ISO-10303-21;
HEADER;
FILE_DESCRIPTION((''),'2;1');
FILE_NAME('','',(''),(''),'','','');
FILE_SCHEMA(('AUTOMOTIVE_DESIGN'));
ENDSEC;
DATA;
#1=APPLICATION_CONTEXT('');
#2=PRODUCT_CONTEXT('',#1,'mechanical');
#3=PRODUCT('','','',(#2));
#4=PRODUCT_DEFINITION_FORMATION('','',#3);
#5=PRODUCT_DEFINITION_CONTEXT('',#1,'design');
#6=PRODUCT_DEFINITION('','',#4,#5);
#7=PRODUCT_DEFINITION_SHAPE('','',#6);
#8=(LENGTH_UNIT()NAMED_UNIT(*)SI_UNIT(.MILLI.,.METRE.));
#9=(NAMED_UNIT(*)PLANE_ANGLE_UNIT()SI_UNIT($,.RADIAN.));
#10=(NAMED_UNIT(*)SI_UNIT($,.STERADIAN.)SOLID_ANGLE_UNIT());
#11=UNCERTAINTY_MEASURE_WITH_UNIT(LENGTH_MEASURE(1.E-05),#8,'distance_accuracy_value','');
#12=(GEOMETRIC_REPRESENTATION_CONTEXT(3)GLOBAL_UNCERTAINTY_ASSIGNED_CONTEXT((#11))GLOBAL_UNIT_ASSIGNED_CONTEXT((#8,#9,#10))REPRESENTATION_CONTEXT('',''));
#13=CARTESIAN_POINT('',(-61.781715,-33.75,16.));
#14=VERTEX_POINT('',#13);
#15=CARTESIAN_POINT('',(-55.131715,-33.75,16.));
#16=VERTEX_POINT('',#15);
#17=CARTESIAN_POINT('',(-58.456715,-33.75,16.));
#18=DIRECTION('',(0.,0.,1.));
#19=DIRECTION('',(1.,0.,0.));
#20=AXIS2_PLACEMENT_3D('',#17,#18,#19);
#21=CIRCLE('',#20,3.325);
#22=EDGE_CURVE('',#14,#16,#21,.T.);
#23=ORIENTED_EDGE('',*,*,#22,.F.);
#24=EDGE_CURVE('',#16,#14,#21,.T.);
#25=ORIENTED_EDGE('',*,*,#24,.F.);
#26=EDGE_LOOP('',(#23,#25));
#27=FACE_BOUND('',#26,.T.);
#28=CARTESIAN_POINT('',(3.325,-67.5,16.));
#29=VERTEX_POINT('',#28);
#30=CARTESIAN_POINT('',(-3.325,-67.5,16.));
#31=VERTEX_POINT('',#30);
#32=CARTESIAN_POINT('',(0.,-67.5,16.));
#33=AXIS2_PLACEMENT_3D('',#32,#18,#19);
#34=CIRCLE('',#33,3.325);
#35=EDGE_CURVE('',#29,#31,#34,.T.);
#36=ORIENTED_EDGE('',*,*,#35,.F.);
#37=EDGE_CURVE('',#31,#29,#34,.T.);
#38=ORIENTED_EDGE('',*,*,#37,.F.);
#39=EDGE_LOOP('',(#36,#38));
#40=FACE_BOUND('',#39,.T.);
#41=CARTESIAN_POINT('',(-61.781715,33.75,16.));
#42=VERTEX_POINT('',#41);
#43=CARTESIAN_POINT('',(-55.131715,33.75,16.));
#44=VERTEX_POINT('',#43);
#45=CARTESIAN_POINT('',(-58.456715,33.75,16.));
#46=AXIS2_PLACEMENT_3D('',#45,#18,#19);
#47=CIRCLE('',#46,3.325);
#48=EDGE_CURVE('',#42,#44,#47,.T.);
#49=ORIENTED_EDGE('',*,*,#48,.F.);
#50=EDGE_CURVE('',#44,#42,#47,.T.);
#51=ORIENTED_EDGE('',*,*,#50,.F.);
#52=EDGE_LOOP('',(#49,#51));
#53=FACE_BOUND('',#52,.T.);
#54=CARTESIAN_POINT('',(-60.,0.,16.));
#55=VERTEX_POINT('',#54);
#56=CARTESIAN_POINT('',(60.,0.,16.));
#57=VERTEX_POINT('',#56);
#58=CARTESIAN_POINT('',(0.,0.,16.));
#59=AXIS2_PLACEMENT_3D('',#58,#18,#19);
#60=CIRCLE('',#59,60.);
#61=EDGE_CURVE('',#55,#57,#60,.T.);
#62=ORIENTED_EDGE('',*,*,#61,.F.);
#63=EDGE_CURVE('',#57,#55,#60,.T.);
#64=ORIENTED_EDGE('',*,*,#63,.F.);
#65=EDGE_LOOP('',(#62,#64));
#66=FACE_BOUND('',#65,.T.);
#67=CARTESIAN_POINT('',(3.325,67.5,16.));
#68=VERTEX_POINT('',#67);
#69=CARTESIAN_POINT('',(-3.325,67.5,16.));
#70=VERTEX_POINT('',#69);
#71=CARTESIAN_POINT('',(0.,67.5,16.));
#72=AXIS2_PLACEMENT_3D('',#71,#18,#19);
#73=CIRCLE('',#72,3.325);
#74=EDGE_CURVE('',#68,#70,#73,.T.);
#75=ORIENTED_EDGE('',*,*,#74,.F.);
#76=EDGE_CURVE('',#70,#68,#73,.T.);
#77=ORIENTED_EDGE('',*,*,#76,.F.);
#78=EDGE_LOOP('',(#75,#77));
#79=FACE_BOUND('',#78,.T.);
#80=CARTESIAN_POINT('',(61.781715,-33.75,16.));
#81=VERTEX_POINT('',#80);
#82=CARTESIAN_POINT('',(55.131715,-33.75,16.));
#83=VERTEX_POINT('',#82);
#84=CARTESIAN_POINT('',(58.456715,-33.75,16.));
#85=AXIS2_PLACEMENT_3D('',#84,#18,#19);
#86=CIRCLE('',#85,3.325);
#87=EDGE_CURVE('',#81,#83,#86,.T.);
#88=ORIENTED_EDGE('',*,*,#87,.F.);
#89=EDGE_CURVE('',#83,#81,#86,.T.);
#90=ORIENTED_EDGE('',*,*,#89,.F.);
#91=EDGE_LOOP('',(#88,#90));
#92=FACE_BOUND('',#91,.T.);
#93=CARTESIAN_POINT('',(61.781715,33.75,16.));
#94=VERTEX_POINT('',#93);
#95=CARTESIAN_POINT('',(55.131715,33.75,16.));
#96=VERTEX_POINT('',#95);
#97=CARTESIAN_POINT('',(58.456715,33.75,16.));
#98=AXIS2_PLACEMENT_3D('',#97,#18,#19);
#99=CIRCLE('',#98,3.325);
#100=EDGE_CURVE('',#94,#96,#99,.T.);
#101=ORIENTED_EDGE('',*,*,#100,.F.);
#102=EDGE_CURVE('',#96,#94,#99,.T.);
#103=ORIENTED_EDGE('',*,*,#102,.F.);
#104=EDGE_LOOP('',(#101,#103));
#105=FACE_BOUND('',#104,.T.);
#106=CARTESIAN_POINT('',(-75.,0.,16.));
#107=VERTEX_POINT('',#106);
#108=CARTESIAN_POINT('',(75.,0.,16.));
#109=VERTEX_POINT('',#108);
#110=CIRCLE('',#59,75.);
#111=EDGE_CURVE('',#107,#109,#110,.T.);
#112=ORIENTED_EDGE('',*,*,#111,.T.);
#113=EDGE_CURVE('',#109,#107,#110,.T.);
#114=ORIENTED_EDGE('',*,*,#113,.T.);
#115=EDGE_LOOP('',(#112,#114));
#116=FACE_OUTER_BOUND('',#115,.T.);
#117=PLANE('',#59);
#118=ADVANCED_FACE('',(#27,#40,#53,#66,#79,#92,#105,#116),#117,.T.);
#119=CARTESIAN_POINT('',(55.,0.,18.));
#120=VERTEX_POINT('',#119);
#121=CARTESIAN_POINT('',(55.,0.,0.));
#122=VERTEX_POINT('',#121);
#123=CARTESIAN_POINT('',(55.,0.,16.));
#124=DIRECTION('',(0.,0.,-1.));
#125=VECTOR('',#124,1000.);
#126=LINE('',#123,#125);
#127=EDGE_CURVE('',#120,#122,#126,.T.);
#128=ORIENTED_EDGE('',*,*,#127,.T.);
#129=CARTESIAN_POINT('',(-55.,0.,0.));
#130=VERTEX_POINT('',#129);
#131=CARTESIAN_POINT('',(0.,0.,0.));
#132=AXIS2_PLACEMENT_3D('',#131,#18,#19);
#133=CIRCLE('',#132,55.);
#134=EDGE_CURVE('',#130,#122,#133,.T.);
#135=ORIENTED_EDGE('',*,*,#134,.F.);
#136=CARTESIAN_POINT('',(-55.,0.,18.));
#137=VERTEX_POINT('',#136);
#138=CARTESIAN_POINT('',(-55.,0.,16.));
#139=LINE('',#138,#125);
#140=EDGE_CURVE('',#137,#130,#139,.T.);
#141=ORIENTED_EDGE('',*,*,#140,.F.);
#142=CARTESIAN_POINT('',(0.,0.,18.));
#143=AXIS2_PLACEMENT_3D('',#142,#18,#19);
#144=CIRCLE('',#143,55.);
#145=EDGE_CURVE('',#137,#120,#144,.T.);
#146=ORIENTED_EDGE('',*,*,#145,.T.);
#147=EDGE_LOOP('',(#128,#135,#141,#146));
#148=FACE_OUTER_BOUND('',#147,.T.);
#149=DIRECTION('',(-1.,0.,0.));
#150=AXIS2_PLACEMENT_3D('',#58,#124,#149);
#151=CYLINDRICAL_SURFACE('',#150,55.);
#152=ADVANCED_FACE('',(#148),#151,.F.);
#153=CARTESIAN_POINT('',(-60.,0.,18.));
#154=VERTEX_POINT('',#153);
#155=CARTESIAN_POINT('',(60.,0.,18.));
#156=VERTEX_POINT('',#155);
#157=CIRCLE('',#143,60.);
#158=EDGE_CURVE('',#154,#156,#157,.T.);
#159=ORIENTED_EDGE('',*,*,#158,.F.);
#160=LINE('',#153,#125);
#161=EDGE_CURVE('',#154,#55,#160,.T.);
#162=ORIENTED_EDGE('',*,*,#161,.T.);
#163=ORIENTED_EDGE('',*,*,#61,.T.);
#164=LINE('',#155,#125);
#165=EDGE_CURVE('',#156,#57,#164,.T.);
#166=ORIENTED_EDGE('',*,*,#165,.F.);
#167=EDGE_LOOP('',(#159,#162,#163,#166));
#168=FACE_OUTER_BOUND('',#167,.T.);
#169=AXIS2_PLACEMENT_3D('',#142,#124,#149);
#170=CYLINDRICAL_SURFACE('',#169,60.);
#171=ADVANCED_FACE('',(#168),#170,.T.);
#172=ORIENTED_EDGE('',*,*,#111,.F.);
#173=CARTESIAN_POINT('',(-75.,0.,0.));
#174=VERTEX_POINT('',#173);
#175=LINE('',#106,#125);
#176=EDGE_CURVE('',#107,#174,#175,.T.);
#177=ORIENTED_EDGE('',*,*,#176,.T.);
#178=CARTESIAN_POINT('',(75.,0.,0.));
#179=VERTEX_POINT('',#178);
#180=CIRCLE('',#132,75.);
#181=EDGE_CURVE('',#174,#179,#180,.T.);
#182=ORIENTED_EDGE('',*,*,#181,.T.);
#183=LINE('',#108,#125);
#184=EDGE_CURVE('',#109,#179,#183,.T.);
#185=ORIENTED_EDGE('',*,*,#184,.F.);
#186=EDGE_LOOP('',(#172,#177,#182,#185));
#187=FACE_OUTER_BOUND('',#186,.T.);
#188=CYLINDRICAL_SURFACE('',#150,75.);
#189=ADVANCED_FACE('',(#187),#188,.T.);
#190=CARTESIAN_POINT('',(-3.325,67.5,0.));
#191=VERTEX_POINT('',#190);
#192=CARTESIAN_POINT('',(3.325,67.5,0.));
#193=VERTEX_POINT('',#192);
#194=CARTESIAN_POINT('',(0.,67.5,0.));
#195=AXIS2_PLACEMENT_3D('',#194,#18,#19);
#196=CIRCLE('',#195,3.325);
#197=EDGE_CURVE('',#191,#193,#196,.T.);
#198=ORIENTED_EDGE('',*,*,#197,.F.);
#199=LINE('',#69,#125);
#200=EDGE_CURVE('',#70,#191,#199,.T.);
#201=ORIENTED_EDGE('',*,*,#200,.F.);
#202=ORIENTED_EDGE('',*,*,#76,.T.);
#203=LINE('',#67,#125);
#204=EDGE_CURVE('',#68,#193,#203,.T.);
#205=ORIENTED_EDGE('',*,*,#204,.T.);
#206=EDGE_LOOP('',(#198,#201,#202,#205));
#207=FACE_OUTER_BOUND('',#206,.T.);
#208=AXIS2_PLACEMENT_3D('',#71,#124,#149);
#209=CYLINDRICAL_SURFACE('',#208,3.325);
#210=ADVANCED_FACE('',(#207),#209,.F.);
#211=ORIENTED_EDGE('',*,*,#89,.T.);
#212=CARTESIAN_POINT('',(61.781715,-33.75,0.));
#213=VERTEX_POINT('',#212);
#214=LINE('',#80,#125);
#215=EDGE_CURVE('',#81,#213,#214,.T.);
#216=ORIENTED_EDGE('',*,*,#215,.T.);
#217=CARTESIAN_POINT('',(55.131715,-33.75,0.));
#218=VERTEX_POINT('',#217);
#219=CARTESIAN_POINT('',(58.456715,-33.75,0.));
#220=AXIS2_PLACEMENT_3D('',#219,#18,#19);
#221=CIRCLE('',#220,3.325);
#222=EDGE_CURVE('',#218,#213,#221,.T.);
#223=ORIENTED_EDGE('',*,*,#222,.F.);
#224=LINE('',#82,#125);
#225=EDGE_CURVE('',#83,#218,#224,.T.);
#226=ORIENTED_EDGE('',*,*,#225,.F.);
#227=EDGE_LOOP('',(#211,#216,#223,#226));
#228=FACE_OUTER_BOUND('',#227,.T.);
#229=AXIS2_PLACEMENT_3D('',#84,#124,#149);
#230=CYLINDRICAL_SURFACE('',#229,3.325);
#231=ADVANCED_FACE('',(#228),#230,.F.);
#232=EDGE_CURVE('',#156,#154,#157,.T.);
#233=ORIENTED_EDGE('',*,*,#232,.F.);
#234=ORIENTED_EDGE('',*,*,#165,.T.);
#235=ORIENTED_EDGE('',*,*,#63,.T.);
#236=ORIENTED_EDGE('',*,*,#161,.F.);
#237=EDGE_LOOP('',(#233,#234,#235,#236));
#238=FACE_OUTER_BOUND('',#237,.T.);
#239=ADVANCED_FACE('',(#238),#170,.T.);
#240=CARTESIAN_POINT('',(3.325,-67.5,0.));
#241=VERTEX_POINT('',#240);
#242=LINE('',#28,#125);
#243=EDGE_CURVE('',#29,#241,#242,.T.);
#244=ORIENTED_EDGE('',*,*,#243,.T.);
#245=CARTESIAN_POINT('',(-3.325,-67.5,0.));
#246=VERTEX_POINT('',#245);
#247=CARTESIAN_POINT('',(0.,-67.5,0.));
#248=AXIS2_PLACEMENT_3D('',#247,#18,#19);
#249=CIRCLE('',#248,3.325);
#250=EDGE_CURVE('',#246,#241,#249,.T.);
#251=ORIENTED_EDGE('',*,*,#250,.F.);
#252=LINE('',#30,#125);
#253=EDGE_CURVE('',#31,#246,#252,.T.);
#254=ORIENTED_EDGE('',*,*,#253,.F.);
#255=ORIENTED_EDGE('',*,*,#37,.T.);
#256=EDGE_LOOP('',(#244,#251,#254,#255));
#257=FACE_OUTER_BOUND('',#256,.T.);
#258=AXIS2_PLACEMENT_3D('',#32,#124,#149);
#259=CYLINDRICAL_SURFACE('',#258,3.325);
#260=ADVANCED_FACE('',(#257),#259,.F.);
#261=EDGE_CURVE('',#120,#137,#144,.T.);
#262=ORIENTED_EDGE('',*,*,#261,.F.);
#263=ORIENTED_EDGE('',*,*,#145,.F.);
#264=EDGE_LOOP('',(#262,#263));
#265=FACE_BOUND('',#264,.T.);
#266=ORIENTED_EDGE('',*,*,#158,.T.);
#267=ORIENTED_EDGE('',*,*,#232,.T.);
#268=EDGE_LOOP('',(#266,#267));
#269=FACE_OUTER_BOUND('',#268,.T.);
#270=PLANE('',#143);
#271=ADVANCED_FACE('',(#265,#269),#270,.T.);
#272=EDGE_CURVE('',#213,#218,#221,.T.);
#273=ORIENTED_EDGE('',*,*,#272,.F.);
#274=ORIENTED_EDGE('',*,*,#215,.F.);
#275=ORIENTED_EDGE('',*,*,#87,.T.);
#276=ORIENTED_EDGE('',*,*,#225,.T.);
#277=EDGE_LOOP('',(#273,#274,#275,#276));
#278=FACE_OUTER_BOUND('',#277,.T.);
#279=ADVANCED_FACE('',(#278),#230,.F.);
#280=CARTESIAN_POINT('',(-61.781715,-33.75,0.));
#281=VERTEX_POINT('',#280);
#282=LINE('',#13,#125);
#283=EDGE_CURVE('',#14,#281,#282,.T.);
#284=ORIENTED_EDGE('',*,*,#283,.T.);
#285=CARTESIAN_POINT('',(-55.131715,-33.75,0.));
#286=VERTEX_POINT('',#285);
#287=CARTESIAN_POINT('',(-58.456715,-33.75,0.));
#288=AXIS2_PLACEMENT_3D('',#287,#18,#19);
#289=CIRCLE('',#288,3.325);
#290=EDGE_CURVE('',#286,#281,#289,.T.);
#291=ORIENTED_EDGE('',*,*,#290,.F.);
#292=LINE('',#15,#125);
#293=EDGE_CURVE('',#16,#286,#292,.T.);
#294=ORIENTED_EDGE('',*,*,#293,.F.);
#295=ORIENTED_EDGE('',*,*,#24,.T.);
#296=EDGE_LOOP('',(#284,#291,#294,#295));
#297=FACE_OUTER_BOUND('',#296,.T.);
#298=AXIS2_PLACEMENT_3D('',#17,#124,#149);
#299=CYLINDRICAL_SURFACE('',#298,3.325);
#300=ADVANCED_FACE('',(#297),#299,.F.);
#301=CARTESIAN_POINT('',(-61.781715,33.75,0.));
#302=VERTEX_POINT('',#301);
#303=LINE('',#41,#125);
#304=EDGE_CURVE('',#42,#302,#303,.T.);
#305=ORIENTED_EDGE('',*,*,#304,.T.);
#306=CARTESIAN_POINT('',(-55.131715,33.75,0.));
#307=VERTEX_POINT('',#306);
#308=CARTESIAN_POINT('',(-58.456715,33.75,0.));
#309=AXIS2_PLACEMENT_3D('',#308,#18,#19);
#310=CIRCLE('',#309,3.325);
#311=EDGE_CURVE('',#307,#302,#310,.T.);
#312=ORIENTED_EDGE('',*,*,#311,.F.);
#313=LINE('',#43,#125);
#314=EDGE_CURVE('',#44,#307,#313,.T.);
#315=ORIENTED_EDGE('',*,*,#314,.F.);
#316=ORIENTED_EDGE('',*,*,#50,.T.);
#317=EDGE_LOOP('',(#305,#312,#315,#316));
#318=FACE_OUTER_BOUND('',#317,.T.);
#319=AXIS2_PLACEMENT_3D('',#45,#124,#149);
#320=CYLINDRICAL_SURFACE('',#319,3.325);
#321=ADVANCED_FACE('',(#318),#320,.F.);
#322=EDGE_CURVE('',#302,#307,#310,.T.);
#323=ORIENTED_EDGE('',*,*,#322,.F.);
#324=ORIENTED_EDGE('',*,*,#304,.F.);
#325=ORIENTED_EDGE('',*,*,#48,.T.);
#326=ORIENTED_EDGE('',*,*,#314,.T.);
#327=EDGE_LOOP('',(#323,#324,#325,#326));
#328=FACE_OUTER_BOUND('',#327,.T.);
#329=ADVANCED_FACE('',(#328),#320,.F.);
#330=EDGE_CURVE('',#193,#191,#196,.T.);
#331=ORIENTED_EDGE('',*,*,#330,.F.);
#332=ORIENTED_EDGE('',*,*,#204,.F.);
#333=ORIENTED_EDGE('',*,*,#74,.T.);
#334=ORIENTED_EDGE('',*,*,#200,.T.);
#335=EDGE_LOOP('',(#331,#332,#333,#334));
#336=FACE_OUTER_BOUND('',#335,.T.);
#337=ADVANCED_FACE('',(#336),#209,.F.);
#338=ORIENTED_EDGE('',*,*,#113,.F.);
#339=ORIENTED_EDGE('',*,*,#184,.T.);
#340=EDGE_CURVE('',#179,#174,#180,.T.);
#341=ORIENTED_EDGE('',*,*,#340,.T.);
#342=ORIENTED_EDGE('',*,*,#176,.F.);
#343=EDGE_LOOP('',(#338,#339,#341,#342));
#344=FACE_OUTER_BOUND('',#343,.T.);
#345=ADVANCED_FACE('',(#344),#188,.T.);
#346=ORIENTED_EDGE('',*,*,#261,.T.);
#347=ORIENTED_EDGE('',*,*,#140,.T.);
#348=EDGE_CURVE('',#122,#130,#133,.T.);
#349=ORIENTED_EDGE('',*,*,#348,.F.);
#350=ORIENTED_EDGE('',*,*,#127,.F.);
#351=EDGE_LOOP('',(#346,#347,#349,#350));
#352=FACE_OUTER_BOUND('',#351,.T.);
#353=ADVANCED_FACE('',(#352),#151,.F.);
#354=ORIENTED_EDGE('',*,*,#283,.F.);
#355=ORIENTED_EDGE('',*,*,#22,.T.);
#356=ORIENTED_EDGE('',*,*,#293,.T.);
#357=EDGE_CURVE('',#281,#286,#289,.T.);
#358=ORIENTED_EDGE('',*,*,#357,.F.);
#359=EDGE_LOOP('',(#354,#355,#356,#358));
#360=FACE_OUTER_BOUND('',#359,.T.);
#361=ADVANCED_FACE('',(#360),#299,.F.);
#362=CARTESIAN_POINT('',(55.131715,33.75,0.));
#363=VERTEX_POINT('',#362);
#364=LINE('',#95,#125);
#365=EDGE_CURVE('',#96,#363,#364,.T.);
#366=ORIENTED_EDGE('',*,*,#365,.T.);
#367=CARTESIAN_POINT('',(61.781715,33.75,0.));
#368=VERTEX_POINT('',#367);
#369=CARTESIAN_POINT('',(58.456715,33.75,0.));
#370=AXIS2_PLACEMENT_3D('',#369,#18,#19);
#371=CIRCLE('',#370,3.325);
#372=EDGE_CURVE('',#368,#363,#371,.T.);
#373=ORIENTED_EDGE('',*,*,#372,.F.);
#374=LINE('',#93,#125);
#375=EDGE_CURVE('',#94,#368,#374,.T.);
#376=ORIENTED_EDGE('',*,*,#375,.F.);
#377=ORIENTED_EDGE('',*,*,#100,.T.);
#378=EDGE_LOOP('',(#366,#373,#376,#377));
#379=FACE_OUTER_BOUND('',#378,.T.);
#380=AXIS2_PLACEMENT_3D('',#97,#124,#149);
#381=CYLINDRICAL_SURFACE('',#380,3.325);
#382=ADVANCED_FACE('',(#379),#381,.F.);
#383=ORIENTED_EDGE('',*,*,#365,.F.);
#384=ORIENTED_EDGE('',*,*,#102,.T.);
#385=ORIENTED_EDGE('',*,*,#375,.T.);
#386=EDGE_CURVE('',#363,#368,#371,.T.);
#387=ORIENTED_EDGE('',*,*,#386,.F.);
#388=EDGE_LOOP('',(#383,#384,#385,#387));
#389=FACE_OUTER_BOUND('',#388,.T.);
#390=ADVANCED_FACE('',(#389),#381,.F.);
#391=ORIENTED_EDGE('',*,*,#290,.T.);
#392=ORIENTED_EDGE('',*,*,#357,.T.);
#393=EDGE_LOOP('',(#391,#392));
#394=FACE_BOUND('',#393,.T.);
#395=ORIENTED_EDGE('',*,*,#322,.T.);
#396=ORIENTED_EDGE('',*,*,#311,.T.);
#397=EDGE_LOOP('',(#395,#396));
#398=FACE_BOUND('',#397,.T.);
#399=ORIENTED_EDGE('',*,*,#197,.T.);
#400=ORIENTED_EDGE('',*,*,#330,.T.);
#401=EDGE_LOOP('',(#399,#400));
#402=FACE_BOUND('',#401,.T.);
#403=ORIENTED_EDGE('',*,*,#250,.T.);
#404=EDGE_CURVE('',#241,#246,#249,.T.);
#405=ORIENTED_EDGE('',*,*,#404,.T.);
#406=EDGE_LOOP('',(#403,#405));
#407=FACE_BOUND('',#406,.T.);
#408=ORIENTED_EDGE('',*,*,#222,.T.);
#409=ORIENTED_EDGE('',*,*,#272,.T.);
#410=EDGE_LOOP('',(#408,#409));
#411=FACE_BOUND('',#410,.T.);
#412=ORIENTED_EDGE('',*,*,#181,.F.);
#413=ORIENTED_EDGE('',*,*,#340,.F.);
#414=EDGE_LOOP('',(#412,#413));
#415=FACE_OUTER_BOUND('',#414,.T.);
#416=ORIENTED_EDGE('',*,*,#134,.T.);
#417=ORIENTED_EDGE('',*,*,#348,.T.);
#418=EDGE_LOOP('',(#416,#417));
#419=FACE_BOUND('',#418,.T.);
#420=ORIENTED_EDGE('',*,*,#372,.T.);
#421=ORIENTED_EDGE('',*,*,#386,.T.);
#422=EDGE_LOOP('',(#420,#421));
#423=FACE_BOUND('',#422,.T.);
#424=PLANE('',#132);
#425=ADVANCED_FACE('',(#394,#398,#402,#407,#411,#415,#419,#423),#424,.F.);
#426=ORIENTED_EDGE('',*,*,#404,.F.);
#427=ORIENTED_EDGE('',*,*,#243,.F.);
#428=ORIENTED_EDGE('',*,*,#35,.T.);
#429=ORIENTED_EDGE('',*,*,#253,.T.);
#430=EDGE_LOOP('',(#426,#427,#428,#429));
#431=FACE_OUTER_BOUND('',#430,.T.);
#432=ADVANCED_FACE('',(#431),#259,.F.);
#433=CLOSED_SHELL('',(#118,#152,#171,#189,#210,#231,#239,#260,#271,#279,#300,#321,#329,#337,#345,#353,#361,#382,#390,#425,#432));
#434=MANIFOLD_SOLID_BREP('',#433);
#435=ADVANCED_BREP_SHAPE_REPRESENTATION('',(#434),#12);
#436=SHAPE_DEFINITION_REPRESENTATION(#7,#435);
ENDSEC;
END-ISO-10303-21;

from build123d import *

# Parameters (mm, degrees)
SKETCH1_R           = 75
SKETCH1_R_2         = 55
SKETCH1_R_3         = 3.325
BOSS_EXTRUDE1_DEPTH = 16
SKETCH2_R           = 60
SKETCH2_R_2         = 55
BOSS_EXTRUDE2_DEPTH = 2


with BuildPart() as part:
    # Sketch1 → Boss-Extrude1 (new body)
    with BuildSketch(Plane.XY):
        Circle(SKETCH1_R)
        Circle(SKETCH1_R_2, mode=Mode.SUBTRACT)
        with Locations((0, 67.5)):
            Circle(SKETCH1_R_3, mode=Mode.SUBTRACT)
        with Locations((58.456714755, 33.75)):
            Circle(SKETCH1_R_3, mode=Mode.SUBTRACT)
        with Locations((58.456714755, -33.75)):
            Circle(SKETCH1_R_3, mode=Mode.SUBTRACT)
        with Locations((0, -67.5)):
            Circle(SKETCH1_R_3, mode=Mode.SUBTRACT)
        with Locations((-58.456714755, -33.75)):
            Circle(SKETCH1_R_3, mode=Mode.SUBTRACT)
        with Locations((-58.456714755, 33.75)):
            Circle(SKETCH1_R_3, mode=Mode.SUBTRACT)
    extrude(amount=BOSS_EXTRUDE1_DEPTH)

    # Sketch2 → Boss-Extrude2 (add)
    with BuildSketch(Plane.XY.offset(16)):
        Circle(SKETCH2_R)
        Circle(SKETCH2_R_2, mode=Mode.SUBTRACT)
    extrude(amount=BOSS_EXTRUDE2_DEPTH)


solid = part.part
